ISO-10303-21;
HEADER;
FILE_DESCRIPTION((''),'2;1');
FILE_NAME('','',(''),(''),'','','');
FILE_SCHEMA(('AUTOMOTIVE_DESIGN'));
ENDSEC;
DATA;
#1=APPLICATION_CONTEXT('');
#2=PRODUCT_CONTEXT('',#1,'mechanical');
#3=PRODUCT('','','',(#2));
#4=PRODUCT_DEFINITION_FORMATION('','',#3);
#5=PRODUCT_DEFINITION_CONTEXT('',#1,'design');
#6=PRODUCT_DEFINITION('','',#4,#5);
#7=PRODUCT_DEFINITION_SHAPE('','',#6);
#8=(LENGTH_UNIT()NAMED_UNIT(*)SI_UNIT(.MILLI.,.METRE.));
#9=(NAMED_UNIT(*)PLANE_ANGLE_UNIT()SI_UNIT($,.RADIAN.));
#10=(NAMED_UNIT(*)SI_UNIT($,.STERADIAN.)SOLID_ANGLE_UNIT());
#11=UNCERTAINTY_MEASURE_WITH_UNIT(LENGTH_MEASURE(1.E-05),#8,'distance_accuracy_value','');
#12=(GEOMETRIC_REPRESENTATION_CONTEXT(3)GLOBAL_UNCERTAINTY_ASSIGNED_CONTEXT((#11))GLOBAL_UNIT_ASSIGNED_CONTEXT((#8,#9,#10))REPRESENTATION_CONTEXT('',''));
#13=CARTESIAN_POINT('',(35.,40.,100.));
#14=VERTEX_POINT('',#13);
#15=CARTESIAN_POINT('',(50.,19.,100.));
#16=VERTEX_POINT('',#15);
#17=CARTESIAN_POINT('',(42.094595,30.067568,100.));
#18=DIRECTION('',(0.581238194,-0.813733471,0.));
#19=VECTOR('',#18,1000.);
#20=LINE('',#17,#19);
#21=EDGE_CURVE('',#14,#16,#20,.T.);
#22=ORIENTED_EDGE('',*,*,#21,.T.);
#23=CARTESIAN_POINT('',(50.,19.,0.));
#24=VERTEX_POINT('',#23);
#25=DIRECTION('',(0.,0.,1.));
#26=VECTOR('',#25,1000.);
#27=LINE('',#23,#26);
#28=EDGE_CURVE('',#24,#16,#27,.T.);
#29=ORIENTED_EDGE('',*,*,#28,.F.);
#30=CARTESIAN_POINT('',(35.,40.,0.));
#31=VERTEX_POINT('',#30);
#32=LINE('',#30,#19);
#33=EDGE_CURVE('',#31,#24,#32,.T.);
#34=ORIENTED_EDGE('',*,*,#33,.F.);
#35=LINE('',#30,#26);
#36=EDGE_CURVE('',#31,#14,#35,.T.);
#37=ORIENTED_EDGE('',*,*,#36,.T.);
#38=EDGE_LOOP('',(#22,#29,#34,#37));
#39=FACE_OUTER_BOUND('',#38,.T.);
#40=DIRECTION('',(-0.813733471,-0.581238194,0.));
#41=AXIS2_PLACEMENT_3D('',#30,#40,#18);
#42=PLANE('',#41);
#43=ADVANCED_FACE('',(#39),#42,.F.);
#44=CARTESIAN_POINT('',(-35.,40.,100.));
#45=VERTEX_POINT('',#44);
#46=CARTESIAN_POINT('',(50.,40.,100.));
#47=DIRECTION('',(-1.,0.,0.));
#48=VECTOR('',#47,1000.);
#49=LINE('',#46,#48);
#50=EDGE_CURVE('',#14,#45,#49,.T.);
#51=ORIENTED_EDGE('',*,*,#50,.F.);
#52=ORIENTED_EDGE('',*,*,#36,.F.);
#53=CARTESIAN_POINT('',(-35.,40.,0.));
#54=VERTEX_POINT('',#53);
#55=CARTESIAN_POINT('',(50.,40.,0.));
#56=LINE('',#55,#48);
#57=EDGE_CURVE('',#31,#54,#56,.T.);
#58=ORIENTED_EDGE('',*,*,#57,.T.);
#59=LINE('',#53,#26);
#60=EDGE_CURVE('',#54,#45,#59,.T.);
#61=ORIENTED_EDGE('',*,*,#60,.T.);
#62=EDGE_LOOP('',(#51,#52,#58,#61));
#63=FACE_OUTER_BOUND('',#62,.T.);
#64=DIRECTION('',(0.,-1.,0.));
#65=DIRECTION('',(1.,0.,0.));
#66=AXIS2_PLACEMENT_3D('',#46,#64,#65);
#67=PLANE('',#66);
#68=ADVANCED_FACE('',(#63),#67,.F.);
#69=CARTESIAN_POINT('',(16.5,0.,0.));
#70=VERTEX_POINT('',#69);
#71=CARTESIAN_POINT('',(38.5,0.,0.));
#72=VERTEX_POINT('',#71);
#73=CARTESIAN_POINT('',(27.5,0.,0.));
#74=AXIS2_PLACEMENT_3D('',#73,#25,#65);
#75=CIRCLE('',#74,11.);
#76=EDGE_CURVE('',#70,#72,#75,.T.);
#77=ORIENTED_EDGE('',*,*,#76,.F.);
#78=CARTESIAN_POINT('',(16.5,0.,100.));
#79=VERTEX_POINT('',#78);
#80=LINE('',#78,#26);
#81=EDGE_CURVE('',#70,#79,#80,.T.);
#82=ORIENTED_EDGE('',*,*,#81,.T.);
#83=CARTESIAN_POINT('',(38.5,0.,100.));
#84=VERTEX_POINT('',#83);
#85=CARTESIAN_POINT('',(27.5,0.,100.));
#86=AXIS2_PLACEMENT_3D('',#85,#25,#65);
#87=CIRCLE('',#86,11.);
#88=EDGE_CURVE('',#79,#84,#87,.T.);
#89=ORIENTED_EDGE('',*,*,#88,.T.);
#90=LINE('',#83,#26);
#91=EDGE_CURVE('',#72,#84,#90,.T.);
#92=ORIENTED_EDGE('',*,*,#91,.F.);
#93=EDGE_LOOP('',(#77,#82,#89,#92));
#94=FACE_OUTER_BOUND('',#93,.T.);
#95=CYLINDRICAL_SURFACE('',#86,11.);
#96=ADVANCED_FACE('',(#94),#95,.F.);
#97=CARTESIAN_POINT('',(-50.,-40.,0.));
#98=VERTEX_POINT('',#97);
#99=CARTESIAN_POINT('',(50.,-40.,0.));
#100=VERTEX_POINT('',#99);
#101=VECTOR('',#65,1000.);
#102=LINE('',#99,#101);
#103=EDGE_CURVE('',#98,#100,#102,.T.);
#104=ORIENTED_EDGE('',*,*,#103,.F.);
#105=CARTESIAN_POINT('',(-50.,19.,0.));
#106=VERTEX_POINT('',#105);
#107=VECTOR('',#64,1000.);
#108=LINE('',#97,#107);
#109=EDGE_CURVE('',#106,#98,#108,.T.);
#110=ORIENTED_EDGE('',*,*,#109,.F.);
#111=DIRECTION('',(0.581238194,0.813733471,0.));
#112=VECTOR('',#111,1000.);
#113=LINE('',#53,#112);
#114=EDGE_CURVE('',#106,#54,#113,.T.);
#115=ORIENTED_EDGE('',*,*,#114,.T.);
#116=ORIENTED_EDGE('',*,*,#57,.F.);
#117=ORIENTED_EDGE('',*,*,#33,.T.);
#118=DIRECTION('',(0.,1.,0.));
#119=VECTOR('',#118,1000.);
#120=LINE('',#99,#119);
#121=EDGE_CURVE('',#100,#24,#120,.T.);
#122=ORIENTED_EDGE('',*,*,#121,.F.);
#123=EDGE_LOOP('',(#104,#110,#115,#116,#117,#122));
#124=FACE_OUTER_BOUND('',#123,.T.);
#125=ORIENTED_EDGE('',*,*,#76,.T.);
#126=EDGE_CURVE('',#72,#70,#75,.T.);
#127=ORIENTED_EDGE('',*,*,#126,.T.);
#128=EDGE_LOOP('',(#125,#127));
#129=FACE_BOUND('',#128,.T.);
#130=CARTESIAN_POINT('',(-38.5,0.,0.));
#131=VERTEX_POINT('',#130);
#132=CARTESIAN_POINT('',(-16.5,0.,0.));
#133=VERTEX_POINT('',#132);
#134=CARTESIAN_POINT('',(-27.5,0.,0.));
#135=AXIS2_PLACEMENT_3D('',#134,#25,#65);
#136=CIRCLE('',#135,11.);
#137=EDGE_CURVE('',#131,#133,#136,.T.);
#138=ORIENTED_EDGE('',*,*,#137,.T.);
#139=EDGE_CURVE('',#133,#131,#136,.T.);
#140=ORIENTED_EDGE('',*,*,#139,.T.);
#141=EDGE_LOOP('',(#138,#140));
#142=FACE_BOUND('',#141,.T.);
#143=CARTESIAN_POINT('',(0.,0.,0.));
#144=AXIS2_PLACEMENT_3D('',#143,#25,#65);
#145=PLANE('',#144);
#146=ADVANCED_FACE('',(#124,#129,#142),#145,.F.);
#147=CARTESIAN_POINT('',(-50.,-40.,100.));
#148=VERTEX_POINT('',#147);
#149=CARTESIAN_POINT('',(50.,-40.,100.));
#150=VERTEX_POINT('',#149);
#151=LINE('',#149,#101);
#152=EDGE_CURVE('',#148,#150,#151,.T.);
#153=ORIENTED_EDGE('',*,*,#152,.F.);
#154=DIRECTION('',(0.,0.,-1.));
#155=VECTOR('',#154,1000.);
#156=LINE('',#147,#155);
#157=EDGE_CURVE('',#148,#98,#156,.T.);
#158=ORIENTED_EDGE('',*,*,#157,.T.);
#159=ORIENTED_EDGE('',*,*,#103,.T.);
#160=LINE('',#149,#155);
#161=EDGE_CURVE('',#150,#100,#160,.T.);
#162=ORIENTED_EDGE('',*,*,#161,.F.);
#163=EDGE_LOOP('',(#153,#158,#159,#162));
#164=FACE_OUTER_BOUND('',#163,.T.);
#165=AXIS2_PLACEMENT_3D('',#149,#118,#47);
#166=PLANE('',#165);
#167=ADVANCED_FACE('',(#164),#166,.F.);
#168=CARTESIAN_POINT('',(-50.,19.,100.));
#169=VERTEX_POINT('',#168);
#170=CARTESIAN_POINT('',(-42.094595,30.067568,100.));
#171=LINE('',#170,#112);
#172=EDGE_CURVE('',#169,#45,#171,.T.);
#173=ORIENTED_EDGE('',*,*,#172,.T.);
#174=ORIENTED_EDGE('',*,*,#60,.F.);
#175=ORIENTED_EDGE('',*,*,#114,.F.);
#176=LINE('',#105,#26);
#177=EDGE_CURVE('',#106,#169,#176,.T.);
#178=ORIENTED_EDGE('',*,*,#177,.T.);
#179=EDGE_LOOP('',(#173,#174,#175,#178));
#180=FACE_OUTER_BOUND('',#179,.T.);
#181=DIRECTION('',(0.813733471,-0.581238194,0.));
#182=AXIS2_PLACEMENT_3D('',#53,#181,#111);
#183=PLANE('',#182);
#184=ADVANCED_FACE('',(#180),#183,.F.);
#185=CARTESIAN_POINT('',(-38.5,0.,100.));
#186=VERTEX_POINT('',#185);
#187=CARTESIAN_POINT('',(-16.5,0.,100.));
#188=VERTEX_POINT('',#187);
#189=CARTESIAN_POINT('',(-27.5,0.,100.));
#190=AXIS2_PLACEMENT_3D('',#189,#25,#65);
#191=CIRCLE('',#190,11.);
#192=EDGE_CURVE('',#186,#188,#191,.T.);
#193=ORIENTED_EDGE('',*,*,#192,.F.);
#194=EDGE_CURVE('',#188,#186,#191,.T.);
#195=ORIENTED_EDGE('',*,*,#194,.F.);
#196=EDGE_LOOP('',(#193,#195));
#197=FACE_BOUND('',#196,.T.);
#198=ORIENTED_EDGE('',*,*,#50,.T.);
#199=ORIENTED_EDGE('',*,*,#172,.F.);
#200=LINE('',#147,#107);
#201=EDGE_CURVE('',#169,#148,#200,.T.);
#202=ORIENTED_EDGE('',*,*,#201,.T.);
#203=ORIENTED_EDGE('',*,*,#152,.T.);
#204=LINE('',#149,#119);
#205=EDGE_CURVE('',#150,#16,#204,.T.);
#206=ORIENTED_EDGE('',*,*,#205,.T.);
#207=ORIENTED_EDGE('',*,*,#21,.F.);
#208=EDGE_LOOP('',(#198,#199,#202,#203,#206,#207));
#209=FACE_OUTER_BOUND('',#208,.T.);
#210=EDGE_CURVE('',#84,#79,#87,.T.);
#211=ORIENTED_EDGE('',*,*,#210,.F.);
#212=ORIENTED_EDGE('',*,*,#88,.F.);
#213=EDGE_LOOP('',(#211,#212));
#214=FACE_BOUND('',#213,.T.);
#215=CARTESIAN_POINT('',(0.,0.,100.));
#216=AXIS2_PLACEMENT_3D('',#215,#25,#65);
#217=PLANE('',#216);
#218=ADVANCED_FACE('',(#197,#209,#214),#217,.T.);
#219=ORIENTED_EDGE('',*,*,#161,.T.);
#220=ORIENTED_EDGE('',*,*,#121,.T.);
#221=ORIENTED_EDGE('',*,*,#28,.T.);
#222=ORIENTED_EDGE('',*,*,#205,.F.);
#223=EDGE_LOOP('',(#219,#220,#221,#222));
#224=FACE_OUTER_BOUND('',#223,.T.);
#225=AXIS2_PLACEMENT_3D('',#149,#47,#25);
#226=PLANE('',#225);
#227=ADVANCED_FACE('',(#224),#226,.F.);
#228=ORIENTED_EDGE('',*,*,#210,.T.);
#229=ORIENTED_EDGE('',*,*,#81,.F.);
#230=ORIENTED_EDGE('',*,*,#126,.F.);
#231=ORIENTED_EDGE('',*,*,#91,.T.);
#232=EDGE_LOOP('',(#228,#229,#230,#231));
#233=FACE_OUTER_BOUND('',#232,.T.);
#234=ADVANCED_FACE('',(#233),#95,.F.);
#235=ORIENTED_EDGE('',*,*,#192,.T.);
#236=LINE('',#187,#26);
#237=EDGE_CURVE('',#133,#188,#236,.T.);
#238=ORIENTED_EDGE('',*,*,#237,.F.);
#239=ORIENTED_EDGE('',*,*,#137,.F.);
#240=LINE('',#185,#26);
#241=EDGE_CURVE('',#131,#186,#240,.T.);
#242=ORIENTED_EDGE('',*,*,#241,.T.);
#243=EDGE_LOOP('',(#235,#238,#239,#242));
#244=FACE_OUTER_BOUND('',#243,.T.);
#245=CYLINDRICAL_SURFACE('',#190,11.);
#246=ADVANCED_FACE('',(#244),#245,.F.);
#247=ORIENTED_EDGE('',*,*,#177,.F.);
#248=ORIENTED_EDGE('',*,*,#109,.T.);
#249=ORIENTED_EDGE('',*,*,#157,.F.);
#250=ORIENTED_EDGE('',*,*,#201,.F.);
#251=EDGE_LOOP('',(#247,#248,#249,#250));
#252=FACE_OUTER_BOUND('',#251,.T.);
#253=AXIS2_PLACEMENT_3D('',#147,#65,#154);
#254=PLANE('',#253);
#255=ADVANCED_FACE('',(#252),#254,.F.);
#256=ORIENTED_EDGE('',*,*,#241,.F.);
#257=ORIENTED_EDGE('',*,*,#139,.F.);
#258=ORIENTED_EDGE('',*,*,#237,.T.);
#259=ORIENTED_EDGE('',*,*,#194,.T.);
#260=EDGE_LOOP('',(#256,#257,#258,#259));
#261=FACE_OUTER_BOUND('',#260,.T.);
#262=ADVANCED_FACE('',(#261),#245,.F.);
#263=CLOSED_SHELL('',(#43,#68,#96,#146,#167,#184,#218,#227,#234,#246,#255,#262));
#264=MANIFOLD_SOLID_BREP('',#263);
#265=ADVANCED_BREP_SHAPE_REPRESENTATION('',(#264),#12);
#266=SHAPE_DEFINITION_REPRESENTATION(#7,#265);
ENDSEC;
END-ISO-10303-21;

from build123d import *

# Parameters (mm, degrees)
SKETCH1_W               = 100
SKETCH1_H               = 80
BOSS_EXTRUDE1_DEPTH     = 100
CHAMFER1_SIZE           = 10
F_22_DIAMETER_HOLE1_D   = 22
CUT_EXTRUDE1_DEPTH      = 119.74342087
CUT_EXTRUDE1_DEPTH_BACK = 119.74342087


with BuildPart() as part:
    # Sketch1 → Boss-Extrude1 (new body)
    with BuildSketch(Plane.XY):
        Rectangle(SKETCH1_W, SKETCH1_H)
    extrude(amount=BOSS_EXTRUDE1_DEPTH)

    # Chamfer1
    chamfer1_edges = [part.edges().sort_by_distance(p)[0] for p in [
        (-50, 40, 50),
        (50, 40, 50),
    ]]
    chamfer(chamfer1_edges, length=CHAMFER1_SIZE)

    # Ø22 Diameter Hole1 (through all)
    with Locations(Plane.XY.offset(100)):
        with Locations((-27.5, 0), (27.5, 0)):
            Hole(F_22_DIAMETER_HOLE1_D / 2)

    # Sketch4 → Cut-Extrude1 (cut, two sides: drawn at the far end of the back side and taken through both)
    with BuildSketch(Plane.XY.offset(100).offset(-CUT_EXTRUDE1_DEPTH_BACK)):
        Polygon((-35, 40), (-50, 19), (-50, 40), align=None)
        Polygon((50, 40), (35, 40), (50, 19), align=None)
    extrude(amount=CUT_EXTRUDE1_DEPTH + CUT_EXTRUDE1_DEPTH_BACK, mode=Mode.SUBTRACT)


solid = part.part
